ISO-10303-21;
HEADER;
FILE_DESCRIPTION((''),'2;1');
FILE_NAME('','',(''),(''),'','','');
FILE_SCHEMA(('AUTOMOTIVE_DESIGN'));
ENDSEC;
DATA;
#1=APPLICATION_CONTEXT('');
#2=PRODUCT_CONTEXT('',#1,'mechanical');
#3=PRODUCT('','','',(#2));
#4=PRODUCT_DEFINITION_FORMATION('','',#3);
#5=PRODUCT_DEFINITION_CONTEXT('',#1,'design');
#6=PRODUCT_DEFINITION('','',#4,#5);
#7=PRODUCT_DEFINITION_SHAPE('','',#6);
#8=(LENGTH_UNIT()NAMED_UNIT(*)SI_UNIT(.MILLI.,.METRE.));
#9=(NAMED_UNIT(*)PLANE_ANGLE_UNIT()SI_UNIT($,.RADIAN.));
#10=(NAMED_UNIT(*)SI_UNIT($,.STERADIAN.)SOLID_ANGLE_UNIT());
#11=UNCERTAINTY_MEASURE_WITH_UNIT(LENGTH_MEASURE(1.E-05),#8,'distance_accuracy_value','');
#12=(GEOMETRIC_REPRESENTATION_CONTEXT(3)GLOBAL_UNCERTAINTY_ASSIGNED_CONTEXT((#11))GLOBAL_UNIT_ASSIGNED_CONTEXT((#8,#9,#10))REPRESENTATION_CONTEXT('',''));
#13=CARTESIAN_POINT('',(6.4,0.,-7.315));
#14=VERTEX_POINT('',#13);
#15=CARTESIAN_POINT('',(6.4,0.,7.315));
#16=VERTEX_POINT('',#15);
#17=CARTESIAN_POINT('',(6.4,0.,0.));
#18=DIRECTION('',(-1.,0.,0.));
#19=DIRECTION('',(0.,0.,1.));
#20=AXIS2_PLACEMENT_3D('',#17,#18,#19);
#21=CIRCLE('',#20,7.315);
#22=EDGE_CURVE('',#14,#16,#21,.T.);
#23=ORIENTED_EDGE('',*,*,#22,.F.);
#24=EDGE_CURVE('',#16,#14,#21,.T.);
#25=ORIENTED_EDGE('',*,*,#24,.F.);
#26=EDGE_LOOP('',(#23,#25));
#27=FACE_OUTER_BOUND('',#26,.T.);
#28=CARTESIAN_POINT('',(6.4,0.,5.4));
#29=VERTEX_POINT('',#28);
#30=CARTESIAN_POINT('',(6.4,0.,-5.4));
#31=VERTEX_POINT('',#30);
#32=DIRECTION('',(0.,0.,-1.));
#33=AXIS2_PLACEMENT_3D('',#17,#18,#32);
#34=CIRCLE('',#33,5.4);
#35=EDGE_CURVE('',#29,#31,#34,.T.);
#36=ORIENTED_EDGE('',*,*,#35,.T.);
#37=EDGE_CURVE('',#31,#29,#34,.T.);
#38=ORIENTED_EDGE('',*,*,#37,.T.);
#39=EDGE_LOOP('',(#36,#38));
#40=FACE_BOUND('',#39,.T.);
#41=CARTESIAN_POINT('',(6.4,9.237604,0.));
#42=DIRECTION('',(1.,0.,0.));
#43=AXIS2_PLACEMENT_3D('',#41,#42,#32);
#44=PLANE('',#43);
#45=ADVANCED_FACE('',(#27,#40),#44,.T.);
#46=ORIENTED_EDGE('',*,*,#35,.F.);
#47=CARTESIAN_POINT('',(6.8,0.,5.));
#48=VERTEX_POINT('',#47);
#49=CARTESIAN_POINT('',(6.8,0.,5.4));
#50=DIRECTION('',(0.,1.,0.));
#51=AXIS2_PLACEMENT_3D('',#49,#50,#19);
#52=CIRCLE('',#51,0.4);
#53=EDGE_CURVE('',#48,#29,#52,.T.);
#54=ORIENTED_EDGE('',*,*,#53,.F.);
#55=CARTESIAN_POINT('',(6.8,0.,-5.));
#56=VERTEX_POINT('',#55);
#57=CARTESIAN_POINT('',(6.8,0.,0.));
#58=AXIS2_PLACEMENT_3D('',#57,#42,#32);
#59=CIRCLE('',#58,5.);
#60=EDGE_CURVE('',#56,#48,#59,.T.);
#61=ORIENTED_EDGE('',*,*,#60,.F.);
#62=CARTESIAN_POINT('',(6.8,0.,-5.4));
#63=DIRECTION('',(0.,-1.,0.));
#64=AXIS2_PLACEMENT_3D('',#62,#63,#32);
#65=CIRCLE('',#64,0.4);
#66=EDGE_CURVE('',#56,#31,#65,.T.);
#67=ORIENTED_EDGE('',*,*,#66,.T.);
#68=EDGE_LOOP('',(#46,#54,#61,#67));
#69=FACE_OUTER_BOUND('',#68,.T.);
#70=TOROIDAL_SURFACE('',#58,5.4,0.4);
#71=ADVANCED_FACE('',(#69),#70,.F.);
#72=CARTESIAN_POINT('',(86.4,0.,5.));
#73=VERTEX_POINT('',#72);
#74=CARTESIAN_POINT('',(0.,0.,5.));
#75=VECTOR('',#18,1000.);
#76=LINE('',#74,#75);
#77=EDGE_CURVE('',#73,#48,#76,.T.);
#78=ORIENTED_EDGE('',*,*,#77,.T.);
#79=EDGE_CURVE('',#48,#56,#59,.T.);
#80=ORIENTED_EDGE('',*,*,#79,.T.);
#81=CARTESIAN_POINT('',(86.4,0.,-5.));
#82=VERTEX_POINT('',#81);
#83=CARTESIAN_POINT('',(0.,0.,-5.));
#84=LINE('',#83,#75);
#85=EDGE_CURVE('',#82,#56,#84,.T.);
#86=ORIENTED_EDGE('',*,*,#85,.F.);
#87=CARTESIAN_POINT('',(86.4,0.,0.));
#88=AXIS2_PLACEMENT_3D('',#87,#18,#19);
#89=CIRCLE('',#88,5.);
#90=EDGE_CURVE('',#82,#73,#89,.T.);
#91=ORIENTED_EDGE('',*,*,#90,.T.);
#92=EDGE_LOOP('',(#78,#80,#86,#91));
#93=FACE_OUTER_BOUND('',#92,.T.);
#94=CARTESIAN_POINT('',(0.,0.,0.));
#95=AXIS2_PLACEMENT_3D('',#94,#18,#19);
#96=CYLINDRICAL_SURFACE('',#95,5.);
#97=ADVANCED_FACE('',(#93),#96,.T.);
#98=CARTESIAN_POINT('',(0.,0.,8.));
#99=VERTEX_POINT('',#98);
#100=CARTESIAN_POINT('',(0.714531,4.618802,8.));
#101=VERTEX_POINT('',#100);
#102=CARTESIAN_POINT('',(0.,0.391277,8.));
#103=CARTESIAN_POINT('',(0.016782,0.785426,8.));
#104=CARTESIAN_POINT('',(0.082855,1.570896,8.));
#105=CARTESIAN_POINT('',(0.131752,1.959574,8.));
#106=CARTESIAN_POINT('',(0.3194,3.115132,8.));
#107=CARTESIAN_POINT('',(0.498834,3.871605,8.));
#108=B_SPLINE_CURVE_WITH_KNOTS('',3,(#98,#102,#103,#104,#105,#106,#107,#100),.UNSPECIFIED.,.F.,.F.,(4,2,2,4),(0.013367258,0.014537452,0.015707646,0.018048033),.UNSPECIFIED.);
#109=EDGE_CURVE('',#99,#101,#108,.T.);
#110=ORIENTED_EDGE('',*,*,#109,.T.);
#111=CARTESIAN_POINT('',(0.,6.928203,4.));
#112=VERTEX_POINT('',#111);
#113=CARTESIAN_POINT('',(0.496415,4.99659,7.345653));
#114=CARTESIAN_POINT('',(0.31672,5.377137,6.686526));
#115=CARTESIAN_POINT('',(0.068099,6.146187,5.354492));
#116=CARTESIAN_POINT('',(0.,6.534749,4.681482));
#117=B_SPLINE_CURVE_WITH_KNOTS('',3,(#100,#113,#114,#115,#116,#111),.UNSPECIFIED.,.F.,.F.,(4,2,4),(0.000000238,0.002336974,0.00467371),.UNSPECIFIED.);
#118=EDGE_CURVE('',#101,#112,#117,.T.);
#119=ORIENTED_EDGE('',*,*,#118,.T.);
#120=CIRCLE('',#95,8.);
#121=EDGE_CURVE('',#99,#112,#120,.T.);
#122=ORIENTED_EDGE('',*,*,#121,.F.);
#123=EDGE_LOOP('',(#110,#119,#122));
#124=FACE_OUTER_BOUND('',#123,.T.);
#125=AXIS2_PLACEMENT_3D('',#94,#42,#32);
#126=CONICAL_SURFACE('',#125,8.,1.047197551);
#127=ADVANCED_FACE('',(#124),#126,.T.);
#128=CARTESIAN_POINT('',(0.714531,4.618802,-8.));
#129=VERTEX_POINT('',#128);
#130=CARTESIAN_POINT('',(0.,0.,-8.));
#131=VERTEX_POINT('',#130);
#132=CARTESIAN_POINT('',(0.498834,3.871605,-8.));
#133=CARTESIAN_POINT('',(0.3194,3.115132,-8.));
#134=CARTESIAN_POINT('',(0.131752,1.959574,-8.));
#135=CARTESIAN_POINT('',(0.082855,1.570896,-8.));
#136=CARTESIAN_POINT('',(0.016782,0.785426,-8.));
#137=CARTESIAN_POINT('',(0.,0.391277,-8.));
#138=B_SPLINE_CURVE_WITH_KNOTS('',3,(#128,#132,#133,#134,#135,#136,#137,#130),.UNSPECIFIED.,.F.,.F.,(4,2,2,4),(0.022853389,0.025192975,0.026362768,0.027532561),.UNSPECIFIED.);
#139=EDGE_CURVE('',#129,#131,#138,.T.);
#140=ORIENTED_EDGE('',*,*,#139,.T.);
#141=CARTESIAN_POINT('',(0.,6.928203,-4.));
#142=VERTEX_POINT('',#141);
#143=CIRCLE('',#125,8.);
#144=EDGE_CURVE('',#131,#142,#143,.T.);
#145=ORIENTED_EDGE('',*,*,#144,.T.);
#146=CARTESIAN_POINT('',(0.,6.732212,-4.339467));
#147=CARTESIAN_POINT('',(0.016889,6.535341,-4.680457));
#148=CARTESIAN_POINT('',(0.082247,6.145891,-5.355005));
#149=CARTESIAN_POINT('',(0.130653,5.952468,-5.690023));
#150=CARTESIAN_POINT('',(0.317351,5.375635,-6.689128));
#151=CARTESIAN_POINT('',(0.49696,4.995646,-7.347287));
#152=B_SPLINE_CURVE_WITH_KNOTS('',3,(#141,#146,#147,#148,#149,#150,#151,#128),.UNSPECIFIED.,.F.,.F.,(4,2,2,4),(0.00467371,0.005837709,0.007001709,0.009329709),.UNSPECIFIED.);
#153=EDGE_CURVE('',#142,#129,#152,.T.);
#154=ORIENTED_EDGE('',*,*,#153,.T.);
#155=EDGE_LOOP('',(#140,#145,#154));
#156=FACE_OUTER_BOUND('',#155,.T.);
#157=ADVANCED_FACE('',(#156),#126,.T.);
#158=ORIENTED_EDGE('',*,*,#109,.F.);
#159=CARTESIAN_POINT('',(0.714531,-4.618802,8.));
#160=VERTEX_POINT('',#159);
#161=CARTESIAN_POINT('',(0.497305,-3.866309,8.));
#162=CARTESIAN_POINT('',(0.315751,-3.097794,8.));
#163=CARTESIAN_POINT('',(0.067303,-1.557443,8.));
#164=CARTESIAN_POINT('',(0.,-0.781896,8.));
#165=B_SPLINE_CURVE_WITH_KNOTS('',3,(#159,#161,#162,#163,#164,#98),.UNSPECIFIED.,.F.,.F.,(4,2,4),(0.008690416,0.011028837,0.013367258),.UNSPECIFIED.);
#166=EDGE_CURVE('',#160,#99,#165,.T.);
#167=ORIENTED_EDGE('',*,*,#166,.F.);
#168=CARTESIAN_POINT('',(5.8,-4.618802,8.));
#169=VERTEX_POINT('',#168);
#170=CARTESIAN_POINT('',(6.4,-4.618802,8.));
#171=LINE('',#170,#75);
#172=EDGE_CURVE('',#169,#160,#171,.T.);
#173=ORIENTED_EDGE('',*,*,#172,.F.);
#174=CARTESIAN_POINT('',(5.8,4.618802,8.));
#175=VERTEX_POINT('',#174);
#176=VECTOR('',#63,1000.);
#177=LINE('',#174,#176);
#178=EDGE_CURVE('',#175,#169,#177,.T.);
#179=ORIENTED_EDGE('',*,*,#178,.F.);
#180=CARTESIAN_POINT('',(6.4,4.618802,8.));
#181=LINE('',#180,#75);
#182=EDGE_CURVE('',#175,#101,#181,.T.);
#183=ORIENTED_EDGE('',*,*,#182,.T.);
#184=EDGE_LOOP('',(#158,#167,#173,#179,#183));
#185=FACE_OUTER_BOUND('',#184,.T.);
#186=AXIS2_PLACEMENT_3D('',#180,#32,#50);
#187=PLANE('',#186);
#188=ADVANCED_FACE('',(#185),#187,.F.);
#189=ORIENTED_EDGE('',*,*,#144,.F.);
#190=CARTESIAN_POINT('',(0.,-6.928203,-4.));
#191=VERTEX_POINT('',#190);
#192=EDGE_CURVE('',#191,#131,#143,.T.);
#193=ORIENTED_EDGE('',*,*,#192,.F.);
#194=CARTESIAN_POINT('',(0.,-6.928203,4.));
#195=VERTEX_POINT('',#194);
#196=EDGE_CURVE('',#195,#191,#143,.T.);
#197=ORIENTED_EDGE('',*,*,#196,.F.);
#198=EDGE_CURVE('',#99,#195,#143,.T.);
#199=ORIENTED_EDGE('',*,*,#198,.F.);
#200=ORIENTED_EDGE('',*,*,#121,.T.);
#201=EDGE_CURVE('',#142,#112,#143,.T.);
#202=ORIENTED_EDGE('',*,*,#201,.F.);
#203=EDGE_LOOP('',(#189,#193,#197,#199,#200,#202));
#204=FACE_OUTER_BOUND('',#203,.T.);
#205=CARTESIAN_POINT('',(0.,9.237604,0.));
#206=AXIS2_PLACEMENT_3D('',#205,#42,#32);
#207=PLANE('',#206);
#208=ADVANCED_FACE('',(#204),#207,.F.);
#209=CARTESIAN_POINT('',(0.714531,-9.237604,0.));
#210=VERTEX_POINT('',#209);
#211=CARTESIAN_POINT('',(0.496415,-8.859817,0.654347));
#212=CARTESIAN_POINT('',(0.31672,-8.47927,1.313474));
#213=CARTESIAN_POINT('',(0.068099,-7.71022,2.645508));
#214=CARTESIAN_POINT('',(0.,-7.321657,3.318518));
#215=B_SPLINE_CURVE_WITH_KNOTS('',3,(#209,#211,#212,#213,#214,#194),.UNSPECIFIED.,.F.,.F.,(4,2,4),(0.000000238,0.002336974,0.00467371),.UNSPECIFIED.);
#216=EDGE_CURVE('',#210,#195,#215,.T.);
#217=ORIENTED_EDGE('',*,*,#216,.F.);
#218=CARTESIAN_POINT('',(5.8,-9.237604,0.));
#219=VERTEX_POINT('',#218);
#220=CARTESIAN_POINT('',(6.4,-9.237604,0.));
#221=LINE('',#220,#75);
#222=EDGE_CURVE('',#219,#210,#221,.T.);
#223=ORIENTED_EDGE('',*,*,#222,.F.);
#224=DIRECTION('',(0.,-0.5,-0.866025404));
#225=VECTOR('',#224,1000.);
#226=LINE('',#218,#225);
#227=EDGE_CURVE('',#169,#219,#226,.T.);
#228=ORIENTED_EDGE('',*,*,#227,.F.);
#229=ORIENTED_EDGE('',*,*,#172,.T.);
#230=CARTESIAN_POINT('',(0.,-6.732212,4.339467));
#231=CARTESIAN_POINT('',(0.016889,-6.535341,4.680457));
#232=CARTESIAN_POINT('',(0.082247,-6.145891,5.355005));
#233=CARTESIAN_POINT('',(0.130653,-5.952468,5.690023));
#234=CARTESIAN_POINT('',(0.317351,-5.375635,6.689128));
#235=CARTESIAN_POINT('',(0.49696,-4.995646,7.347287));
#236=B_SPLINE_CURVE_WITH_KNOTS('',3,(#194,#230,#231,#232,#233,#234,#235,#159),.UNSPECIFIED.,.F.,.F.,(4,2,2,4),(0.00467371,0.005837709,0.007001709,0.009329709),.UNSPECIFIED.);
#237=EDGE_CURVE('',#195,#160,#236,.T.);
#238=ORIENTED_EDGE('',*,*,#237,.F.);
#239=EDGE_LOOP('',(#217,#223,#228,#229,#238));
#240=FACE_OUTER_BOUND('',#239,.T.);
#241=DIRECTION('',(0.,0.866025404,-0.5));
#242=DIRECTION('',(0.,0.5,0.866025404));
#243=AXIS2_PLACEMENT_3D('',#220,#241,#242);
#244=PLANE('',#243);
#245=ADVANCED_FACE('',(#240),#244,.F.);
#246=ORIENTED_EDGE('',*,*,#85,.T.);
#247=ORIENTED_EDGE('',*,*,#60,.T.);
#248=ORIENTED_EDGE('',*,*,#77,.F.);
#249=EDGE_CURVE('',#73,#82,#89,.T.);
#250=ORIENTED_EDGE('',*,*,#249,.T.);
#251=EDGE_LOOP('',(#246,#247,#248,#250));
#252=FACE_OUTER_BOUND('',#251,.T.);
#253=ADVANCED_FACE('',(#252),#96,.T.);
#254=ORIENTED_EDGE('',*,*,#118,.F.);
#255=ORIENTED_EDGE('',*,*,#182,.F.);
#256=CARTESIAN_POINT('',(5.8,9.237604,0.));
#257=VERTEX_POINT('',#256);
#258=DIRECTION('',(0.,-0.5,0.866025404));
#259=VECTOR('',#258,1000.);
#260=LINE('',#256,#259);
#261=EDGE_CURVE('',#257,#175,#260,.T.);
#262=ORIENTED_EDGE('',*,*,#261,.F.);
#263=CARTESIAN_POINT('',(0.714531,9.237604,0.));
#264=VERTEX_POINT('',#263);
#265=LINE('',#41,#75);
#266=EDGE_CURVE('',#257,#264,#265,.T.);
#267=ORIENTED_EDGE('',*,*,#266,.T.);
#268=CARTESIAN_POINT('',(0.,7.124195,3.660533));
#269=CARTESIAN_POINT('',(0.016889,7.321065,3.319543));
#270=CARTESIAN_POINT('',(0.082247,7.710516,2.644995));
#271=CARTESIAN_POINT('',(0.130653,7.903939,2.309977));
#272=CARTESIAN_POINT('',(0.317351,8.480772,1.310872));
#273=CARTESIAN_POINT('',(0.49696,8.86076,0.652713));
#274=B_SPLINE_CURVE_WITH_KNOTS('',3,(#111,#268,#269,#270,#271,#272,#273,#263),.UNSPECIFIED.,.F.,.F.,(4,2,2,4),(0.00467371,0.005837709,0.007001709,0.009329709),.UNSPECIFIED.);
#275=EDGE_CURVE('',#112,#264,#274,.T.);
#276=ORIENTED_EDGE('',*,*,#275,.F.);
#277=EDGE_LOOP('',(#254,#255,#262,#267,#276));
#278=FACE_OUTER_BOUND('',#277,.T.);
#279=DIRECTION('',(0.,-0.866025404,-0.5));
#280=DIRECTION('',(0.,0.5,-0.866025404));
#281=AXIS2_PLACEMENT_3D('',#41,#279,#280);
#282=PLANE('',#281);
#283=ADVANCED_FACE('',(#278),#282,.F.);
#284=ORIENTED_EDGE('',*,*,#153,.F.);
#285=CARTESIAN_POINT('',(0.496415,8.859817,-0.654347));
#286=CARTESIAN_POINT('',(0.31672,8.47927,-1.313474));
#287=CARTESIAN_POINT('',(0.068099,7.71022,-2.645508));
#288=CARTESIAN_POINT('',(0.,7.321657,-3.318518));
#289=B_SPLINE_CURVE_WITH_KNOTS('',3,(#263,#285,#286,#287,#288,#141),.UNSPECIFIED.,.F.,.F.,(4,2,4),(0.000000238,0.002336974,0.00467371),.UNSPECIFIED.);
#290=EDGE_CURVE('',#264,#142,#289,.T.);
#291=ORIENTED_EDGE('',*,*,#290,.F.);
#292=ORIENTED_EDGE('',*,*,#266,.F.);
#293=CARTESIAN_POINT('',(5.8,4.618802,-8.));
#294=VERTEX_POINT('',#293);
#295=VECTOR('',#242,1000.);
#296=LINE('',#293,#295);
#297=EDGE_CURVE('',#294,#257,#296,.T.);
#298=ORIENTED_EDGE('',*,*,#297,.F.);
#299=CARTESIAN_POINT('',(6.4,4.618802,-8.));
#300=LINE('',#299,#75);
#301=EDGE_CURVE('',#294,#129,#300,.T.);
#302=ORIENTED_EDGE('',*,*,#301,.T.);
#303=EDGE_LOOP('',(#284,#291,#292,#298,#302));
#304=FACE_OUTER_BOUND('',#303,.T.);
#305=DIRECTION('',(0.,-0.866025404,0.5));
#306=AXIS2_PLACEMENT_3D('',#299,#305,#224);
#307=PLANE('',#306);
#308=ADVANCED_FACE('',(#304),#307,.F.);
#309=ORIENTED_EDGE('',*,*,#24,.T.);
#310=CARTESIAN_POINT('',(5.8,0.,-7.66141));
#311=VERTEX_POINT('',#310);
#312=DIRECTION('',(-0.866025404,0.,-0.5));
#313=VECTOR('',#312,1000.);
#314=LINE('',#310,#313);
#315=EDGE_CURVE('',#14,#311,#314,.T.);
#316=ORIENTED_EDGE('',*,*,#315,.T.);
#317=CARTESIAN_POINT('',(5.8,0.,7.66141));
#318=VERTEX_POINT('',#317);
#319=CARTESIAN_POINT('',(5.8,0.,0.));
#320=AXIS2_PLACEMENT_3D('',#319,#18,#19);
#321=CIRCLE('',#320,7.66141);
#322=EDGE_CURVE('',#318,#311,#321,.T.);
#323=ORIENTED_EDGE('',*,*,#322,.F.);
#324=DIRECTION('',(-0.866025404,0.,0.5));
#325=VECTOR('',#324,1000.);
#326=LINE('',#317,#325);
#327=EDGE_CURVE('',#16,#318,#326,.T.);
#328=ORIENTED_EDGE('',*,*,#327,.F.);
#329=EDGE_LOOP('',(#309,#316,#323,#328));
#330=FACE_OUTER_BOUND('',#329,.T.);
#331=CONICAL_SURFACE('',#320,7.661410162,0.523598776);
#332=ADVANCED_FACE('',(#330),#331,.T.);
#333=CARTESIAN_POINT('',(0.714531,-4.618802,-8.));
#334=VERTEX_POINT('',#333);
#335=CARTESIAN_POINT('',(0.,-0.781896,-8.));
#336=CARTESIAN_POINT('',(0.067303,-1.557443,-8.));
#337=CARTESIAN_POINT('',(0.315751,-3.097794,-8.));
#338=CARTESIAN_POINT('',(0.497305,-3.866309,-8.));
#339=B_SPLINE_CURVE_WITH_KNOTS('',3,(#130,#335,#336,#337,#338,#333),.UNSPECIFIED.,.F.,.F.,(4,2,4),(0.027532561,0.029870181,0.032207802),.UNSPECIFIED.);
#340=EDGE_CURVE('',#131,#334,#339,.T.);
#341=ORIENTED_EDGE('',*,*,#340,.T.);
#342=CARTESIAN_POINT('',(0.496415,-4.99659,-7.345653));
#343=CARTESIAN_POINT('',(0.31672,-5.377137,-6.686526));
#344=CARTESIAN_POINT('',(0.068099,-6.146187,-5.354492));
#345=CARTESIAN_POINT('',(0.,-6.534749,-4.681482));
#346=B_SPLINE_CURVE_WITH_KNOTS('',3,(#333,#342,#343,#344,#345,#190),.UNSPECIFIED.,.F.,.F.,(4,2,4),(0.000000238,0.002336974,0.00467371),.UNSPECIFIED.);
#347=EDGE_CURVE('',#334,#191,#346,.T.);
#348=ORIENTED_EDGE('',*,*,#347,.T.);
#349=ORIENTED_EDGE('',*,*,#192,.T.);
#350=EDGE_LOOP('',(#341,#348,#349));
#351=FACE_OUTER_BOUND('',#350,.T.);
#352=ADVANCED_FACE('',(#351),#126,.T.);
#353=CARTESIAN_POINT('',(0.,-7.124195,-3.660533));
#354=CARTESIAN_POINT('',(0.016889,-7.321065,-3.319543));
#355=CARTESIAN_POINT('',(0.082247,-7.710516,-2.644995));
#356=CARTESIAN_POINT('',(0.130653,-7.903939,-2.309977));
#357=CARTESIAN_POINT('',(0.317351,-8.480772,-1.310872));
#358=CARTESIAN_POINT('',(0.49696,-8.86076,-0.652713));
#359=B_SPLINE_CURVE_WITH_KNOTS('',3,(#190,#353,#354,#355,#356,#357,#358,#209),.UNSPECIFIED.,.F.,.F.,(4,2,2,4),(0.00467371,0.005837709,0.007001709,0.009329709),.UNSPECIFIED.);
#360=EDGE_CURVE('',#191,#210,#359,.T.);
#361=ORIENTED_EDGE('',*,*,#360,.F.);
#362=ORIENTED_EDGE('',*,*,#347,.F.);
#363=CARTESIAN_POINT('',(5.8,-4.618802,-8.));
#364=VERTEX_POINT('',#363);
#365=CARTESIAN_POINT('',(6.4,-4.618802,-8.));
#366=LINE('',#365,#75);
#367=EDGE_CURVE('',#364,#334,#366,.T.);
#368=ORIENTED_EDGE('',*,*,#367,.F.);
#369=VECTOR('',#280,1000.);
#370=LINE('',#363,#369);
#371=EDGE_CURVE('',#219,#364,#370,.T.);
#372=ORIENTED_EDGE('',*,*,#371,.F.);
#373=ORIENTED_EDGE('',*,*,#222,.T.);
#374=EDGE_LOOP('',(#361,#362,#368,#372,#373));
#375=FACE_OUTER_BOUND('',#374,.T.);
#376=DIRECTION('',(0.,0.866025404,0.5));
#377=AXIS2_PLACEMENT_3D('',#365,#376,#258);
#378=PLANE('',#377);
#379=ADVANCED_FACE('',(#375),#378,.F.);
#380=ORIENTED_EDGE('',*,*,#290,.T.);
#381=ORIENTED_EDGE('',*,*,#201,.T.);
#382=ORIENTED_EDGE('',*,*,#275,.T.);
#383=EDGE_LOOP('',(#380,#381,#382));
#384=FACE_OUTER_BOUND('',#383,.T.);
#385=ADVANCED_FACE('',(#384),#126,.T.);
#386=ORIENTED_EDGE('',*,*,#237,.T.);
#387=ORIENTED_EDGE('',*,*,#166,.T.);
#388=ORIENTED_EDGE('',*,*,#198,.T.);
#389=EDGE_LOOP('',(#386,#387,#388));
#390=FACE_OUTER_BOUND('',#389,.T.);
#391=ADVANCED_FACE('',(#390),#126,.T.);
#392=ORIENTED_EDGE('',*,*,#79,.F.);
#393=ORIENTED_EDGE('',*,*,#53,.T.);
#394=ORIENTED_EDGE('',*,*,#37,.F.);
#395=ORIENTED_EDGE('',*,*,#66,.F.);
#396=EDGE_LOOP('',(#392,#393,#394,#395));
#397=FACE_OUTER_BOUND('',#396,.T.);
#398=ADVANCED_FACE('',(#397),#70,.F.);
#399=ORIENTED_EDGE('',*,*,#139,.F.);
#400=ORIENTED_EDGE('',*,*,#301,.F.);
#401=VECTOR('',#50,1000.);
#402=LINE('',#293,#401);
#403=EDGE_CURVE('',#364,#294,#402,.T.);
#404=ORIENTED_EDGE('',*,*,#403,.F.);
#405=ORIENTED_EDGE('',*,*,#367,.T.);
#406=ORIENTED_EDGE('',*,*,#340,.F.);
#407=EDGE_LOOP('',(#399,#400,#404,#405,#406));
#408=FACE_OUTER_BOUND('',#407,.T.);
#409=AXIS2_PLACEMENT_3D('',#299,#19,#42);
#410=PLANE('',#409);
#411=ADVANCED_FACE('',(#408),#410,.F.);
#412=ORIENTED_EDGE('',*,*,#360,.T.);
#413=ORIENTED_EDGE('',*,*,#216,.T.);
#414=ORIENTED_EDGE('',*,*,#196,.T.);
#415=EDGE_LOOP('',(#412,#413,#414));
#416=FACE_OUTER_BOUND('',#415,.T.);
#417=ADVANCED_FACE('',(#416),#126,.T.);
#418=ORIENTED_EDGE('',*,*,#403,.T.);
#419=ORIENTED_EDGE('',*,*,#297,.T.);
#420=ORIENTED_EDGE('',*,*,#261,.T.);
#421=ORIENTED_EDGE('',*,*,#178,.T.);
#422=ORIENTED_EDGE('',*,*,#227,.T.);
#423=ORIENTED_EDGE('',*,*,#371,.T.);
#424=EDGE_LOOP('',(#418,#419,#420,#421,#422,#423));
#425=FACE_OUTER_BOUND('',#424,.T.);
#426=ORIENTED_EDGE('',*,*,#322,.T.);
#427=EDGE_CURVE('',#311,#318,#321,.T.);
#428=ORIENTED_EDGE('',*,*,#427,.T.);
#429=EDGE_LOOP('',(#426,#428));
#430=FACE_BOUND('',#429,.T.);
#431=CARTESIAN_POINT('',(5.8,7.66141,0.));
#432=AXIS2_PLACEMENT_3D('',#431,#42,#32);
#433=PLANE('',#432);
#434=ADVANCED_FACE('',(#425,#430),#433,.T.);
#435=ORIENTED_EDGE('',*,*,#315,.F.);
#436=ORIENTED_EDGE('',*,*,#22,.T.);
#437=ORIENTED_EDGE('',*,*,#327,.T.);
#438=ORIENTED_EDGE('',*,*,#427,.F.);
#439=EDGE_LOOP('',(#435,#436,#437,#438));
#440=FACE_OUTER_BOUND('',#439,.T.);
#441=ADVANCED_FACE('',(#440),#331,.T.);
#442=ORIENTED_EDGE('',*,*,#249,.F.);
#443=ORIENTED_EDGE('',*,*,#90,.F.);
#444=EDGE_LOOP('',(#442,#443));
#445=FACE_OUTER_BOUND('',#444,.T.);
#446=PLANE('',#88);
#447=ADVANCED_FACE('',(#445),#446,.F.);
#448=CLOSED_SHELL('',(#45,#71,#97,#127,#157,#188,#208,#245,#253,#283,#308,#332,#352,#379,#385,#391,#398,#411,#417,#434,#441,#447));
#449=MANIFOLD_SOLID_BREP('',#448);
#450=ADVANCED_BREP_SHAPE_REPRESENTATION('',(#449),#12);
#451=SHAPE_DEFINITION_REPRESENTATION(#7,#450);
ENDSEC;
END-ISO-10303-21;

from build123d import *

# Parameters (mm, degrees)
EXTRUDE_384_DEPTH = 6.4
FILLET_1305_R     = 0.4


with BuildPart() as part:
    # 草图1 → Extrude 384 (new body)
    with BuildSketch(Plane(origin=(0, 0, 0), x_dir=(0, 0, -1), z_dir=(1, 0, 0))):
        Polygon((8, 4.618802154), (8, -4.618802154), (0, -9.237604307), (-8, -4.618802154), (-8, 4.618802154), (0, 9.237604307), align=None)
    extrude(amount=EXTRUDE_384_DEPTH)

    # 草图2 → 凸台-旋转1 (revolve)
    with BuildSketch(Plane.XY, mode=Mode.PRIVATE) as revolve_1_sk:
        Polygon((0, 0), (86.4, 0), (86.4, 3.701), (86.4, 5), (60.4, 5), (0, 5), align=None)
    revolve(revolve_1_sk.sketch.rotate(Axis((0, 0, 0), (1, 0, 0)), 90), axis=Axis((0, 0, 0), (1, 0, 0)))

    # 草图3 → 切除-旋转1 (revolve, cut)
    with BuildSketch(Plane.XY):
        Polygon((0, 8), (3.601282526, 14.237604307), (3.601282526, 19.237604307), (-10, 19.237604307), (-10, 8), align=None)
    revolve(axis=Axis((0, 0, 0), (1, 0, 0)), mode=Mode.SUBTRACT)

    # 草图4 → 切除-旋转3 (revolve, cut)
    with BuildSketch(Plane.XY, mode=Mode.PRIVATE) as cut_revolve_3_sk:
        Polygon((6.4, 7.315), (5.8, 7.661410162), (5.8, 9.237604307), (6.4, 9.237604307), align=None)
    revolve(cut_revolve_3_sk.sketch.rotate(Axis((0, 0, 0), (1, 0, 0)), 90), axis=Axis((0, 0, 0), (1, 0, 0)), mode=Mode.SUBTRACT)

    # Fillet 1305
    fillet_1305_edges = [part.edges().sort_by_distance(p)[0] for p in [
        (6.4, 0, -5),
    ]]
    fillet(fillet_1305_edges, radius=FILLET_1305_R)


solid = part.part
